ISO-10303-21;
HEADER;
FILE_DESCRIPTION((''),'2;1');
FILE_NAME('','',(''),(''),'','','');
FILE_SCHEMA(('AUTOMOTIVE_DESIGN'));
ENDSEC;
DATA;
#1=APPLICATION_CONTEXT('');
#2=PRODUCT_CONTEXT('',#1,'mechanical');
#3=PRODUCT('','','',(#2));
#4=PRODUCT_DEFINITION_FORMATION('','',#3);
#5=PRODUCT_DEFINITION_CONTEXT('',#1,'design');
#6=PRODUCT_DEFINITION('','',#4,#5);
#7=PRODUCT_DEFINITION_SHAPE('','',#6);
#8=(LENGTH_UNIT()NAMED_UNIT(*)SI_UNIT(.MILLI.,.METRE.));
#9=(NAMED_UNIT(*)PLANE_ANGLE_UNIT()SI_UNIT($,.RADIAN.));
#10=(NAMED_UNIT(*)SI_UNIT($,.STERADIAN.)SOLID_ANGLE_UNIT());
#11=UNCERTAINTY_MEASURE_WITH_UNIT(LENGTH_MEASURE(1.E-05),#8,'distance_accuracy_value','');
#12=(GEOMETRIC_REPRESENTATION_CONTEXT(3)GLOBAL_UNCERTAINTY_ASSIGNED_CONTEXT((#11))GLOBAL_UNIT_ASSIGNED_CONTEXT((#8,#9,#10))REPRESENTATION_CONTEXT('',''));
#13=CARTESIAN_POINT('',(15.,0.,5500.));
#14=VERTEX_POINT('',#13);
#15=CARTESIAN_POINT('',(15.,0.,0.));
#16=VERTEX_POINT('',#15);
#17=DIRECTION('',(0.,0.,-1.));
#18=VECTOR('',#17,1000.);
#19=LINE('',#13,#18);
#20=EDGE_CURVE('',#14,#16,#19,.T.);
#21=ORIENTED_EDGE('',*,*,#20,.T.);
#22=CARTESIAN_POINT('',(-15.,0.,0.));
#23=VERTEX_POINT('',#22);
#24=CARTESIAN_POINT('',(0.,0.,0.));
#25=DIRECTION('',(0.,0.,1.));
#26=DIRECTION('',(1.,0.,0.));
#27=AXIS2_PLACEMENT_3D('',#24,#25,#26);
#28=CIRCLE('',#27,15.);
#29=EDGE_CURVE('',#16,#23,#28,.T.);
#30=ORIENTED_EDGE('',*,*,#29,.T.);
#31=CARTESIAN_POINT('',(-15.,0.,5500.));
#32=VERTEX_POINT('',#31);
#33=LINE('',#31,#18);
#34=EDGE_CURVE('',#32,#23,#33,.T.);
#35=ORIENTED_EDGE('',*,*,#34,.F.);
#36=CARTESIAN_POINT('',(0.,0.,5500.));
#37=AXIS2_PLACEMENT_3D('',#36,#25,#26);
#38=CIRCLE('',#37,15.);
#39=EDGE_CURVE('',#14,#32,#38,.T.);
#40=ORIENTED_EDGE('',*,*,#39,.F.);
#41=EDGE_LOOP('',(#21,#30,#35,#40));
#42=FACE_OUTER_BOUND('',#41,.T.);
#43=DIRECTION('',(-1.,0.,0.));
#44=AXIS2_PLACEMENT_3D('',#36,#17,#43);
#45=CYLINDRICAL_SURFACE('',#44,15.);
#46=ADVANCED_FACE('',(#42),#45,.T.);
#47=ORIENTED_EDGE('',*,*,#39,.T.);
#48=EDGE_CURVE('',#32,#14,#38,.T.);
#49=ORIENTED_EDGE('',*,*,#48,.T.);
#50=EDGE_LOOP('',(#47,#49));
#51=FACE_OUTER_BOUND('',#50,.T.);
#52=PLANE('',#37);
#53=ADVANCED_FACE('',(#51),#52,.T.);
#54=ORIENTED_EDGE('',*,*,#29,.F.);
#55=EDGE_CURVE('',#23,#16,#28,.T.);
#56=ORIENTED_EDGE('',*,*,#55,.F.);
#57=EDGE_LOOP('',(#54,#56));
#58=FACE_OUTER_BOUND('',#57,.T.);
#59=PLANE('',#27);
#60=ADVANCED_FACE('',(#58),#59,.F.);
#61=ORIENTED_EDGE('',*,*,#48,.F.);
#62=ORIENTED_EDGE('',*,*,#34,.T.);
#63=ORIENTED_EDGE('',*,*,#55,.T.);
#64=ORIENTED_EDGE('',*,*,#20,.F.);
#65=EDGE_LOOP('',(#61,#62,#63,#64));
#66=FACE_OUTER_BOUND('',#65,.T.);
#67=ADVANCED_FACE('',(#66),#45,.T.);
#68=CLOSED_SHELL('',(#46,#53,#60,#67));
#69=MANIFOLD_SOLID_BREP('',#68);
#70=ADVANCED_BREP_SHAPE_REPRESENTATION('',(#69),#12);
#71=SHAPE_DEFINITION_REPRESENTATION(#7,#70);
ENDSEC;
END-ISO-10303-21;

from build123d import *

# Parameters (mm, degrees)
SKETCH1_R           = 15
BOSS_EXTRUDE1_DEPTH = 5500


with BuildPart() as part:
    # Sketch1 → Boss-Extrude1 (new body)
    with BuildSketch(Plane.XY):
        Circle(SKETCH1_R)
    extrude(amount=BOSS_EXTRUDE1_DEPTH)


solid = part.part
